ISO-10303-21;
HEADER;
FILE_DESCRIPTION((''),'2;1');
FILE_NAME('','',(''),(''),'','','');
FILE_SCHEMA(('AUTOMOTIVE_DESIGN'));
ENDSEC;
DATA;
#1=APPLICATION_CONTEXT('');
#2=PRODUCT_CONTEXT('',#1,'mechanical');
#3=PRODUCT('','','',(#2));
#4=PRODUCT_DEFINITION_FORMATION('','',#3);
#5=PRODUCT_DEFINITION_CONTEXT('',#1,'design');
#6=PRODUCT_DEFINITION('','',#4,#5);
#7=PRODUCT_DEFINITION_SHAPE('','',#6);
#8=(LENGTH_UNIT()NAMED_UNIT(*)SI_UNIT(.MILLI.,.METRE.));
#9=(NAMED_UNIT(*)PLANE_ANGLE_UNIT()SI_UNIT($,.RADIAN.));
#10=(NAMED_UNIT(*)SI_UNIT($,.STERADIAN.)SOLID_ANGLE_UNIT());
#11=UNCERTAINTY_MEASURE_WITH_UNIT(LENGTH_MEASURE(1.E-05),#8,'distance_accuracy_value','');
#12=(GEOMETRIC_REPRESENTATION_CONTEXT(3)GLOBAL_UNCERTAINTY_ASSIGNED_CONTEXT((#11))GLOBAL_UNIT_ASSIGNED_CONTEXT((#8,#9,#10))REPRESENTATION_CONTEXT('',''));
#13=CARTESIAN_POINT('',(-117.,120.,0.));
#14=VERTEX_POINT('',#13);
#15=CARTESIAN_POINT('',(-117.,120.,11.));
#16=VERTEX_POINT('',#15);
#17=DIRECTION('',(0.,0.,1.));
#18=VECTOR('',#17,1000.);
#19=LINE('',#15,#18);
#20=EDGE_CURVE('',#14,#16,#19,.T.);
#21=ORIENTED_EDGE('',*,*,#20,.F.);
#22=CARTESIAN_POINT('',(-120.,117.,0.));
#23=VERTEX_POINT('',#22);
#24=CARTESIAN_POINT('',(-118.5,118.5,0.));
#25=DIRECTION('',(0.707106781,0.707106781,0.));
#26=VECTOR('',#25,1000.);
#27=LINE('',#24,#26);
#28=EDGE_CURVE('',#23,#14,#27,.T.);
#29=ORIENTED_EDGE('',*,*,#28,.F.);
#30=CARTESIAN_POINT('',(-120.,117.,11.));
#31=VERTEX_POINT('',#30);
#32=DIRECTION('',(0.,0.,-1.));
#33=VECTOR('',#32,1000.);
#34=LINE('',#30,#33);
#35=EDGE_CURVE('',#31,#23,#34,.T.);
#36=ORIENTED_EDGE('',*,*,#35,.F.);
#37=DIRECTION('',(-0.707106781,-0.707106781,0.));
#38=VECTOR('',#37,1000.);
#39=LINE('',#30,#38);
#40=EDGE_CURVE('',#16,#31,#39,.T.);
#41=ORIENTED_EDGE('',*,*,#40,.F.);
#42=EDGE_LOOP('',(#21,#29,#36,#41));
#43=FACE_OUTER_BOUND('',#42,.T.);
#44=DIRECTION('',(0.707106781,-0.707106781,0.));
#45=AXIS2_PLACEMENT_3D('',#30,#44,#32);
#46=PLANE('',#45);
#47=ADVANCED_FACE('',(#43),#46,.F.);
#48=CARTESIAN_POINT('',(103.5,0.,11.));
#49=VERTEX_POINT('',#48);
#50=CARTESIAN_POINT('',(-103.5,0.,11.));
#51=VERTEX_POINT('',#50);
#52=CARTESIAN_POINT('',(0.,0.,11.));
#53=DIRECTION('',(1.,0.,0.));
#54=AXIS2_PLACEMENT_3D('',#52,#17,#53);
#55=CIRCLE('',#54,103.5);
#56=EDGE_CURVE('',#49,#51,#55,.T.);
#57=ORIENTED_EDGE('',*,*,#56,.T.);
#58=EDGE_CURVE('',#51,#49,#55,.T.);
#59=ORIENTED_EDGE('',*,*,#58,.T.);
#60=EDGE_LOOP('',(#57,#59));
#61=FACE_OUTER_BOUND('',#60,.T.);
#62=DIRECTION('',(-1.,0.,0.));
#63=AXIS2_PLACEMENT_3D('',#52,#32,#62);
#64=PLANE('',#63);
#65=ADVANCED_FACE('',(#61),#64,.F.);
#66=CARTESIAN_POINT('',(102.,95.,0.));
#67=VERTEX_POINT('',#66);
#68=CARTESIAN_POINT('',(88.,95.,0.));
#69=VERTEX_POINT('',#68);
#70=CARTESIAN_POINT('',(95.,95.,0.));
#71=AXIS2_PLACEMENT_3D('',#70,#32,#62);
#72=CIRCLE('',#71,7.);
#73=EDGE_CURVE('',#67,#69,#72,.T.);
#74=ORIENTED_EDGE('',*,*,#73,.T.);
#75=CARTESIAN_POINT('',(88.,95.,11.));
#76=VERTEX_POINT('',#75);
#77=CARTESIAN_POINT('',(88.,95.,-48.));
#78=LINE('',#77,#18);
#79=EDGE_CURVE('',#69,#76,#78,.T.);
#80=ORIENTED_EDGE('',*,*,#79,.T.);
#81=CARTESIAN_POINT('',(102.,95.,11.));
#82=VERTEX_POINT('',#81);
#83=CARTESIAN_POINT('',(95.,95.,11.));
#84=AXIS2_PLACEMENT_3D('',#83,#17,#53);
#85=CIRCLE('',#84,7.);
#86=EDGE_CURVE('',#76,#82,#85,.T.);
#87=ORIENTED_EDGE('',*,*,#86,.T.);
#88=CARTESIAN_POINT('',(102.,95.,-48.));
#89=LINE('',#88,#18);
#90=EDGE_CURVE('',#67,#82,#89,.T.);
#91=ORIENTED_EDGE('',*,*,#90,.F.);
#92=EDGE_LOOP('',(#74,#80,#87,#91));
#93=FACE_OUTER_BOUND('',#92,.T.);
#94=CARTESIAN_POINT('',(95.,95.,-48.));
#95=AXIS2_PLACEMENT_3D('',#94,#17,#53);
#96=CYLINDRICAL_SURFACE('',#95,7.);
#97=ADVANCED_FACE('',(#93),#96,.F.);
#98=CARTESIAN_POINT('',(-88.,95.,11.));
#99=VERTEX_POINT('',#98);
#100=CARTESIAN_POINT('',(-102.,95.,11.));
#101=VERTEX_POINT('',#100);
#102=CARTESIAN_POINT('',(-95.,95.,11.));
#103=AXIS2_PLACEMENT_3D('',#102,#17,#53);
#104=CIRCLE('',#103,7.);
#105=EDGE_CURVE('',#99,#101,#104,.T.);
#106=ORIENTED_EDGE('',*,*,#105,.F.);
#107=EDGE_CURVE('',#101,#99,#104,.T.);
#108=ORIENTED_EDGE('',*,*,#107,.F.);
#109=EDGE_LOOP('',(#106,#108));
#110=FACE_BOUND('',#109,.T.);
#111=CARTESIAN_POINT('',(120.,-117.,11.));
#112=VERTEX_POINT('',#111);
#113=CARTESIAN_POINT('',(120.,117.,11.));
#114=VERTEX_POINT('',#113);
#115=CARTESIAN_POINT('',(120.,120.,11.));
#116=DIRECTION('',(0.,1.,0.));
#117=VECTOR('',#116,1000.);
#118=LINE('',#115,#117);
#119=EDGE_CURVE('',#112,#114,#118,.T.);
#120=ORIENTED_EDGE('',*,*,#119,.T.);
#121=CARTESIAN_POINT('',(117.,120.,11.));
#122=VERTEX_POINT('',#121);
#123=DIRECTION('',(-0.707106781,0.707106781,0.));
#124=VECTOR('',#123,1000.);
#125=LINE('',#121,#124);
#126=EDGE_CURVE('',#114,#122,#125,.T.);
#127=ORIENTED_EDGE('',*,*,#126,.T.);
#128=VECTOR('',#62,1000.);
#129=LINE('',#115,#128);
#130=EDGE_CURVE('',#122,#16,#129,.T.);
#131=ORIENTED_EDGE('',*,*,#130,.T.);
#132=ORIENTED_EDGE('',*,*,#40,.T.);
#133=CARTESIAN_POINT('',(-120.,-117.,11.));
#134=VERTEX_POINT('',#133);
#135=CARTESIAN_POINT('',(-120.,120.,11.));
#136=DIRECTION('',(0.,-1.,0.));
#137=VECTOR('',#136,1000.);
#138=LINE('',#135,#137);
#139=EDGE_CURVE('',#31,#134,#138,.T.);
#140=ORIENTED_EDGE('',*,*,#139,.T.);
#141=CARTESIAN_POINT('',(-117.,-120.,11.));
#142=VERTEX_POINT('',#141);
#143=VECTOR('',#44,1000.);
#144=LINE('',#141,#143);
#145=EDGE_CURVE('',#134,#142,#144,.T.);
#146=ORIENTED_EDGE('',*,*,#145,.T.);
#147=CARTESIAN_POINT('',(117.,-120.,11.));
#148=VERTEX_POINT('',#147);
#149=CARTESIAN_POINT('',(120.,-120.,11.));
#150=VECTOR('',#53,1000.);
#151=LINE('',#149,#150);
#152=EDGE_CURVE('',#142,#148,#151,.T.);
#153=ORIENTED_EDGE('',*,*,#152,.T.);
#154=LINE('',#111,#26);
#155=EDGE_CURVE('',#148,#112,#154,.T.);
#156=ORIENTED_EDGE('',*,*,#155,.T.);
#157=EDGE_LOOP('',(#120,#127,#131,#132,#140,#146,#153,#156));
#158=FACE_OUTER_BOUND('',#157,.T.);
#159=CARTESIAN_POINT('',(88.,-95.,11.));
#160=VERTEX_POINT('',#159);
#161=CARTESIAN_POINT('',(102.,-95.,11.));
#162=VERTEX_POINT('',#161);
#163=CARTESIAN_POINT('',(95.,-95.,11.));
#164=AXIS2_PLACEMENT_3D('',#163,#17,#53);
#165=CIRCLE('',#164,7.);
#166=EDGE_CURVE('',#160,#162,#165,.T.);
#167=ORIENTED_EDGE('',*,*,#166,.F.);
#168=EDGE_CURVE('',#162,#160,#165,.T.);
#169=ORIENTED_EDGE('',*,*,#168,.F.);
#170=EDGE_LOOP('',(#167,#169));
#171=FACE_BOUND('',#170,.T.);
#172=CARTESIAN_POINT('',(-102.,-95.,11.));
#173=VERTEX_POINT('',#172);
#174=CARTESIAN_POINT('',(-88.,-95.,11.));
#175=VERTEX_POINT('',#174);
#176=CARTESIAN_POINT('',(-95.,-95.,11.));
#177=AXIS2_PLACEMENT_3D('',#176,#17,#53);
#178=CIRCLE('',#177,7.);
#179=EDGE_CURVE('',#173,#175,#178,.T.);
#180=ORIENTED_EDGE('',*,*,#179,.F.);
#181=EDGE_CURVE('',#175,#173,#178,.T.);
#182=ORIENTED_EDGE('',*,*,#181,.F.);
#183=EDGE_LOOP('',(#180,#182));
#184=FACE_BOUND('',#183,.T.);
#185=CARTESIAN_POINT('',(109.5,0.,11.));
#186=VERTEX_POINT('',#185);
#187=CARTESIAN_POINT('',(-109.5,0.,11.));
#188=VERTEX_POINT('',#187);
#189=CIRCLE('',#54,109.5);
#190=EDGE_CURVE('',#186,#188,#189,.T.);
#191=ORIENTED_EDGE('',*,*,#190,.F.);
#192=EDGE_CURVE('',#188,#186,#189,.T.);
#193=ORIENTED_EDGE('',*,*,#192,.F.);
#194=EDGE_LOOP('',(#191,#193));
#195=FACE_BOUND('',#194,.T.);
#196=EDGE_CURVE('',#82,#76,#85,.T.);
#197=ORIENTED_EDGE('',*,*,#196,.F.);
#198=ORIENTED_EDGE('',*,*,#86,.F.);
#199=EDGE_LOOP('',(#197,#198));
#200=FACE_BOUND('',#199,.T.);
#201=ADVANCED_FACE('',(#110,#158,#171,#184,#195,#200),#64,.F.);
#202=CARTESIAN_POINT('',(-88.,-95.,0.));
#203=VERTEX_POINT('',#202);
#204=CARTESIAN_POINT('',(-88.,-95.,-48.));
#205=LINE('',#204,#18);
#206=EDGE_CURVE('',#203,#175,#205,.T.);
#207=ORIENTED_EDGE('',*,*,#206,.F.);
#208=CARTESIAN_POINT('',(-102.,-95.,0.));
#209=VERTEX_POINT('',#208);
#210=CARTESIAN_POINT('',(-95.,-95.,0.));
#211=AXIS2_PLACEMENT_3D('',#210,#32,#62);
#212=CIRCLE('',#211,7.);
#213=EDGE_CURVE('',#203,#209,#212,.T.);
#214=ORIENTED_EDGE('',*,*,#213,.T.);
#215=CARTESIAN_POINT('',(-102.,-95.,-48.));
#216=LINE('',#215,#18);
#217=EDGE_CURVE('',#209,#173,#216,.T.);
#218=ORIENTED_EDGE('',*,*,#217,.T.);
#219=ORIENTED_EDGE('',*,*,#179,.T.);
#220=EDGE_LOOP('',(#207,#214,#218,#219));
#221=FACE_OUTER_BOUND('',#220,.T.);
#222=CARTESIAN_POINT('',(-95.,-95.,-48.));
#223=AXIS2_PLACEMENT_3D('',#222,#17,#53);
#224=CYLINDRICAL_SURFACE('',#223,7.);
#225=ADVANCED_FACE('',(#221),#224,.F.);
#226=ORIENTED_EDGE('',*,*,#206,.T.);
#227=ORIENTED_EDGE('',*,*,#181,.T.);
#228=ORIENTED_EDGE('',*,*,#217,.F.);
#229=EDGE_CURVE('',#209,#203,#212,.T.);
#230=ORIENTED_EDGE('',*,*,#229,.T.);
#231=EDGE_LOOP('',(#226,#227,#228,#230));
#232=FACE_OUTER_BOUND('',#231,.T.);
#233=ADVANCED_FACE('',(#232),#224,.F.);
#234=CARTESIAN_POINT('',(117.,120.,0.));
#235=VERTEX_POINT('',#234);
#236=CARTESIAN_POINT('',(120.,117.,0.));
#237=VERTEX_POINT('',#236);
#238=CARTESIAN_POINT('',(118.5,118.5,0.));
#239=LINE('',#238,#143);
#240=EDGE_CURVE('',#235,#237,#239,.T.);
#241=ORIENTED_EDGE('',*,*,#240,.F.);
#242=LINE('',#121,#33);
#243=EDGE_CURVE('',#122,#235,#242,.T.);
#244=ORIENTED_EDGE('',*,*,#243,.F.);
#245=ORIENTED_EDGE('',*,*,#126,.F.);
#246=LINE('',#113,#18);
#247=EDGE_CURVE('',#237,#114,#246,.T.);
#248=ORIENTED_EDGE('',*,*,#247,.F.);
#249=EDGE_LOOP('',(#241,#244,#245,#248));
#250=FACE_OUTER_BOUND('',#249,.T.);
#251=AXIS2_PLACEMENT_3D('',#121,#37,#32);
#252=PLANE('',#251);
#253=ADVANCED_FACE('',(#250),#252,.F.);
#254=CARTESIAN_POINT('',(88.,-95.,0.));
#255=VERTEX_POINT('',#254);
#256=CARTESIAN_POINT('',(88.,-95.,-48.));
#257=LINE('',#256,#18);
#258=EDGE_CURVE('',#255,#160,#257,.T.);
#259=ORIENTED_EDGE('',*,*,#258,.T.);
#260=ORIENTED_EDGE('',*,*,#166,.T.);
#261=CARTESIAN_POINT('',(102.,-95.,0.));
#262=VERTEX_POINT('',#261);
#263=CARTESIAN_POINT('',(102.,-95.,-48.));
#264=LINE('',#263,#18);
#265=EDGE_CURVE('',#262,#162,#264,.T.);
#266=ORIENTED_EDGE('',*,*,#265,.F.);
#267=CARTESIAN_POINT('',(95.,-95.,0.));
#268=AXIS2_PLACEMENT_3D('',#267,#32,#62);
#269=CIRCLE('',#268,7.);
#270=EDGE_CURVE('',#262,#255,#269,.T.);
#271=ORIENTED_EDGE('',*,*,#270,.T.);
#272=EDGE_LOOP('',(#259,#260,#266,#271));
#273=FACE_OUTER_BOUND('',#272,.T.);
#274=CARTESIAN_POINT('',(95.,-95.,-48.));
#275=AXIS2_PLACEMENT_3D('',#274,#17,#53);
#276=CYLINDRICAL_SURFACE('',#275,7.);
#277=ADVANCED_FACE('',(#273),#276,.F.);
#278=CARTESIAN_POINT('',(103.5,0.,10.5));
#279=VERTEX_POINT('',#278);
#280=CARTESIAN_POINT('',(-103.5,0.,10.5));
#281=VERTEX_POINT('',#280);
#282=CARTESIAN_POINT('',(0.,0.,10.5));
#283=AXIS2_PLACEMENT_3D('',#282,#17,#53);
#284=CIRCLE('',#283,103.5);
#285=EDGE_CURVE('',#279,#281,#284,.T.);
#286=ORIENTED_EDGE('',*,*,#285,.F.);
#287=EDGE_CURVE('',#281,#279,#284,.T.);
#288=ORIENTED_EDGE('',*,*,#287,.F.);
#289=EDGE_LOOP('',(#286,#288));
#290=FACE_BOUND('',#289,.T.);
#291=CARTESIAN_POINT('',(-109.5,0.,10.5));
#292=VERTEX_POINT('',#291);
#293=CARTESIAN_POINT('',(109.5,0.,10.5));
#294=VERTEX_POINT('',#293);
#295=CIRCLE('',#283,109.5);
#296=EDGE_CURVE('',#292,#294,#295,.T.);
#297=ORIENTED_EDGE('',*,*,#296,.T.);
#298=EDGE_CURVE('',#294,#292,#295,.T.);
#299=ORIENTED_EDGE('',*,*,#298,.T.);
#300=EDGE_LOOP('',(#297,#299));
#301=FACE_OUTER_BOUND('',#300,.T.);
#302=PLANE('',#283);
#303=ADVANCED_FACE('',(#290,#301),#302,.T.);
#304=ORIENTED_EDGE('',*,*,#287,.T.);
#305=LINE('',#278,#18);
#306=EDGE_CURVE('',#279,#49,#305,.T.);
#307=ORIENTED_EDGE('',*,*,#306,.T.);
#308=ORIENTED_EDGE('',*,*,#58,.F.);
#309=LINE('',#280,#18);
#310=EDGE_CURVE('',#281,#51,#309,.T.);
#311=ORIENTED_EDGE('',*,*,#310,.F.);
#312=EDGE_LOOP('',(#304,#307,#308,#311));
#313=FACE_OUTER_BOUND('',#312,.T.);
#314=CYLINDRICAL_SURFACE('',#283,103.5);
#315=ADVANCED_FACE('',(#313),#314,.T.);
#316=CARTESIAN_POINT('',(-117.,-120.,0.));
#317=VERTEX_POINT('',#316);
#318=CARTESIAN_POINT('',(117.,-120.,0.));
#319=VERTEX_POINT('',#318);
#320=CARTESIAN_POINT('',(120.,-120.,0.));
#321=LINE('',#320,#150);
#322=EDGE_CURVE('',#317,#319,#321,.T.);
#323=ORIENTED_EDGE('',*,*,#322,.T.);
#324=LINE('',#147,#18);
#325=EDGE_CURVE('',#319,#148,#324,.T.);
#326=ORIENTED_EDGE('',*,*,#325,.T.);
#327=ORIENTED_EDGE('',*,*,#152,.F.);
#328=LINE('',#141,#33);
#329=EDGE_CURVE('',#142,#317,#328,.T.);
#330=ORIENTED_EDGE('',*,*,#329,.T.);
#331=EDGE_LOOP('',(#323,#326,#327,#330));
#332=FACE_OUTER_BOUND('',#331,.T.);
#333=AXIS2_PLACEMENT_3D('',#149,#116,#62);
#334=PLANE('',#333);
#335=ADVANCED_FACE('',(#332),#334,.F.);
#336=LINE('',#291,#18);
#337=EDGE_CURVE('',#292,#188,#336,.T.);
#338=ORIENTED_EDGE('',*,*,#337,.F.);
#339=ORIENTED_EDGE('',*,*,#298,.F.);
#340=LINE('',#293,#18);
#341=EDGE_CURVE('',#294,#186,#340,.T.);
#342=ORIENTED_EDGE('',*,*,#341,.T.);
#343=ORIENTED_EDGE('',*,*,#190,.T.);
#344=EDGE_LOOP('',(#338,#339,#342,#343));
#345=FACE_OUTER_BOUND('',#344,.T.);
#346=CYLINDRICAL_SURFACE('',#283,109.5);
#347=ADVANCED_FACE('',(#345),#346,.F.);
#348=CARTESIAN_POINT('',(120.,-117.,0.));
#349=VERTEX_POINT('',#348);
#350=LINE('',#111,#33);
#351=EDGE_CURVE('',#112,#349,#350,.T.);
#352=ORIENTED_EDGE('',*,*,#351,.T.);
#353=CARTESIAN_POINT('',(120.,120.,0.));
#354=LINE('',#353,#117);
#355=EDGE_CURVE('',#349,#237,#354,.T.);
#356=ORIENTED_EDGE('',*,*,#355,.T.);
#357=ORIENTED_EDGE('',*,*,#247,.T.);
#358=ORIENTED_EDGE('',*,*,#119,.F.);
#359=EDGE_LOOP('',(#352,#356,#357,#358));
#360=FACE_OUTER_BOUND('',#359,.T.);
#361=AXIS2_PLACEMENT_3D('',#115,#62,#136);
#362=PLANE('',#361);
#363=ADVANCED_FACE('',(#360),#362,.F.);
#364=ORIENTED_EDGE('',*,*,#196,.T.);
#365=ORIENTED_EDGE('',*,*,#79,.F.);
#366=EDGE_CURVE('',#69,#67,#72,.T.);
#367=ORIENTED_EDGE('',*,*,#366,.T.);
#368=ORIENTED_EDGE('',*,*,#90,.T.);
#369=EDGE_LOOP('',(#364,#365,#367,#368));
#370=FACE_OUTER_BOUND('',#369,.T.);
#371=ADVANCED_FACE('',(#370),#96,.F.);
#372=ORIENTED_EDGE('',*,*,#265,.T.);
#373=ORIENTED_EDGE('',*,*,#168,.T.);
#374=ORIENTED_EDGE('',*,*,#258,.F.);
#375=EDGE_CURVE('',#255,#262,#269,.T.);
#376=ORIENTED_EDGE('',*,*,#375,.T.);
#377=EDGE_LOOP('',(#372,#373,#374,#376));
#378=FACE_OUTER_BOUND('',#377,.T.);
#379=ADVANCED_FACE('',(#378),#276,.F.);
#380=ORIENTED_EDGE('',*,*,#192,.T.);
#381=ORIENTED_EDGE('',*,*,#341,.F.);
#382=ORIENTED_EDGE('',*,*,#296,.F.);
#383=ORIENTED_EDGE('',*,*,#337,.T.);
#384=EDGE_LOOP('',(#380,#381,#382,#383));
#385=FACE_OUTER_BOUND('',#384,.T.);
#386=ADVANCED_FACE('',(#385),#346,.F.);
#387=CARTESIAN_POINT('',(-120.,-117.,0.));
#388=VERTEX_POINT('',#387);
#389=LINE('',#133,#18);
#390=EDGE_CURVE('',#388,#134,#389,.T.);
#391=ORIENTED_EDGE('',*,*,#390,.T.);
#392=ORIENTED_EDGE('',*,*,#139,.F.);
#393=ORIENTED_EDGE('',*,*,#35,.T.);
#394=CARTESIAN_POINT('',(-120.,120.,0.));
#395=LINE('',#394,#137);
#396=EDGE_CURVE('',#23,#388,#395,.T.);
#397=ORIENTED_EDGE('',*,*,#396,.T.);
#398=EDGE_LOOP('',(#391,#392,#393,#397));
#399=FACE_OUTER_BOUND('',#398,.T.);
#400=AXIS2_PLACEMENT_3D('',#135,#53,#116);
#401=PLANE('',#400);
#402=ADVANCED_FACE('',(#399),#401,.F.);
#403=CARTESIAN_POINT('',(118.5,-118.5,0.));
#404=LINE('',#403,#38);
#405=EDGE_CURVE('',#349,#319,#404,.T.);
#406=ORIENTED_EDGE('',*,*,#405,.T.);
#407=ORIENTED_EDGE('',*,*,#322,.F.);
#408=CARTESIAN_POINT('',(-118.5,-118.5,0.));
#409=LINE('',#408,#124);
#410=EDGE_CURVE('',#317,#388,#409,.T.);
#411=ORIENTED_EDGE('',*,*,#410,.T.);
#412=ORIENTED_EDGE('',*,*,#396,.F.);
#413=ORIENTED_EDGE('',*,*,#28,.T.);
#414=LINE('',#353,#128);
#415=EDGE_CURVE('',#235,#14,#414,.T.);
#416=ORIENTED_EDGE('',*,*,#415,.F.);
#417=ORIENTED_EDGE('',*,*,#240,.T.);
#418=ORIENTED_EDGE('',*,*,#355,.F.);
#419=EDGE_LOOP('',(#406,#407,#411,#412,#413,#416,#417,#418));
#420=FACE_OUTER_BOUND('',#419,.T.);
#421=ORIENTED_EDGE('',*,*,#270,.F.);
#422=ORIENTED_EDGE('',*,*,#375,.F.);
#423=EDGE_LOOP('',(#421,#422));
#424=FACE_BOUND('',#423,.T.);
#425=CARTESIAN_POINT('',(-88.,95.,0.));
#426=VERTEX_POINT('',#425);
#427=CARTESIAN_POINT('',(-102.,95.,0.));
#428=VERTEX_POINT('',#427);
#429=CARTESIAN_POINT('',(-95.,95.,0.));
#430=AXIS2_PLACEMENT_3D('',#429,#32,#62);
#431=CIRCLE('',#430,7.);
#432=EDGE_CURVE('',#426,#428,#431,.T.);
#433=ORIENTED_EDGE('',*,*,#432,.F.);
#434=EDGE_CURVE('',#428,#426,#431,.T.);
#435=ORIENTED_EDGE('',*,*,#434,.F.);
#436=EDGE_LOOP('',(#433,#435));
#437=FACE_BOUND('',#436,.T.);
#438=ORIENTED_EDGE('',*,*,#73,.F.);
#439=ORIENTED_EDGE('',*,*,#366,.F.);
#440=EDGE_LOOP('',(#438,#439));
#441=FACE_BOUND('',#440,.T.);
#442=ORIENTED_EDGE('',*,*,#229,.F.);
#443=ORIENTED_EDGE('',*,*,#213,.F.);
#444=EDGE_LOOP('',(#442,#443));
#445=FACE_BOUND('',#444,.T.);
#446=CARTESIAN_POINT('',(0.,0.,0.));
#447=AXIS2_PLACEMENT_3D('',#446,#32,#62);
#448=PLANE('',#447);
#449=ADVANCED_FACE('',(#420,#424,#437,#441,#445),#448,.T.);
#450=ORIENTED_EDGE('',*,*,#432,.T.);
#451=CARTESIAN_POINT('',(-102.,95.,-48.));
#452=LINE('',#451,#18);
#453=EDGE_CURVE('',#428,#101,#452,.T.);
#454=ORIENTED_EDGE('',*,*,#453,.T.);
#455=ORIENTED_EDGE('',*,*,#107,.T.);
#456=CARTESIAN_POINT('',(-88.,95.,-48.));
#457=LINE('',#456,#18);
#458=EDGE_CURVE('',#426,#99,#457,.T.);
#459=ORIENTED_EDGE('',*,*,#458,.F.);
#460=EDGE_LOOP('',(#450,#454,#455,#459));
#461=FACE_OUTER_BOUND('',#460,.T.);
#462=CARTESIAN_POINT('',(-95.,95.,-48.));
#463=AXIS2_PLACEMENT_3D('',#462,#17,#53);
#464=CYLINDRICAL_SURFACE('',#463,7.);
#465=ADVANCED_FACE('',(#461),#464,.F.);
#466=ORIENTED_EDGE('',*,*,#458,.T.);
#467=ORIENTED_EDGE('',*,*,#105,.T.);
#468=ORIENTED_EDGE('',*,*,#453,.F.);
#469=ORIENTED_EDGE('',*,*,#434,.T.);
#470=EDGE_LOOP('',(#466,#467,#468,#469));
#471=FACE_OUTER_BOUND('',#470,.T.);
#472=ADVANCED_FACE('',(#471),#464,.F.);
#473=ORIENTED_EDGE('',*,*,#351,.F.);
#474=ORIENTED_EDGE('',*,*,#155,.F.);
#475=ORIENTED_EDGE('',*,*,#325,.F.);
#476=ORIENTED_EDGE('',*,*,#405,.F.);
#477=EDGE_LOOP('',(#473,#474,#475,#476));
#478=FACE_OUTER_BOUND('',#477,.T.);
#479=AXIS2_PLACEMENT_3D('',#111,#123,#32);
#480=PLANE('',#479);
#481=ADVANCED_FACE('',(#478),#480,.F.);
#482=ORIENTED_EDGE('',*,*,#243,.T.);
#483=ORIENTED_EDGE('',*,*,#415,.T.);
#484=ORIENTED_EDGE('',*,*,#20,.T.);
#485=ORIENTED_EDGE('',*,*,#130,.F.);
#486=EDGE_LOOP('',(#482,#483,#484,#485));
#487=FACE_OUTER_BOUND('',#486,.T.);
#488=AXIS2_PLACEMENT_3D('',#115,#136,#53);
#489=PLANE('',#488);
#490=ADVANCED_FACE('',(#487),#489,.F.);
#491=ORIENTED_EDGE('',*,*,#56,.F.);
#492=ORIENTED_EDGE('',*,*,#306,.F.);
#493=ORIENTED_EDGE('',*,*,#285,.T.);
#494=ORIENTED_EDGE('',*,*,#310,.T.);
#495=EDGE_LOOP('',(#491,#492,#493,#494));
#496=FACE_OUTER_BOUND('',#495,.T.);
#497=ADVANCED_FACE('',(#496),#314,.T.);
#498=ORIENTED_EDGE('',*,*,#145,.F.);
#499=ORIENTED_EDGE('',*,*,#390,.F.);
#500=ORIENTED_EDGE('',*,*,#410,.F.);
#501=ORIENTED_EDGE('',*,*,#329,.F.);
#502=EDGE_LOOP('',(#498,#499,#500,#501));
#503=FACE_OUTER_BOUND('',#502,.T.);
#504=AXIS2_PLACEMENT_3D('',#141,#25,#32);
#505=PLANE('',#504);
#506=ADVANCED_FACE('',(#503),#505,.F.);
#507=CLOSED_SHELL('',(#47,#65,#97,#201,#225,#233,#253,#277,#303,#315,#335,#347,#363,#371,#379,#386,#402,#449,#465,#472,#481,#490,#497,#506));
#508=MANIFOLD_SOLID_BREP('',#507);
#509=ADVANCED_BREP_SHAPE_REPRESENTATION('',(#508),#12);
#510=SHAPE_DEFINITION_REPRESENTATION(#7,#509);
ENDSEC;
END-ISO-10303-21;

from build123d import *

# Parameters (mm, degrees)
SKETCH1_W           = 240
SKETCH1_H           = 240
BOSS_EXTRUDE1_DEPTH = 11
SKETCH2_R           = 109.5
SKETCH2_R_2         = 103.5
CUT_EXTRUDE1_DEPTH  = 0.5
SKETCH3_R           = 7
CUT_EXTRUDE2_DEPTH  = 59
CHAMFER1_SIZE       = 3


with BuildPart() as part:
    # Sketch1 → Boss-Extrude1 (new body)
    with BuildSketch(Plane.XY):
        Rectangle(SKETCH1_W, SKETCH1_H)
    extrude(amount=BOSS_EXTRUDE1_DEPTH)

    # Sketch2 → Cut-Extrude1 (cut)
    with BuildSketch(Plane.XY.offset(11)):
        Circle(SKETCH2_R)
        Circle(SKETCH2_R_2, mode=Mode.SUBTRACT)
    extrude(amount=-CUT_EXTRUDE1_DEPTH, mode=Mode.SUBTRACT)

    # Sketch3 → Cut-Extrude2 (cut)
    with BuildSketch(Plane.XY.offset(11)):
        with Locations((-95, 95)):
            Circle(SKETCH3_R)
        with Locations((95, 95)):
            Circle(SKETCH3_R)
        with Locations((95, -95)):
            Circle(SKETCH3_R)
        with Locations((-95, -95)):
            Circle(SKETCH3_R)
    extrude(amount=-CUT_EXTRUDE2_DEPTH, mode=Mode.SUBTRACT)

    # Chamfer1
    chamfer1_edges = [part.edges().sort_by_distance(p)[0] for p in [
        (-120, 120, 5.5),
        (120, 120, 5.5),
        (120, -120, 5.5),
        (-120, -120, 5.5),
    ]]
    chamfer(chamfer1_edges, length=CHAMFER1_SIZE)


solid = part.part
